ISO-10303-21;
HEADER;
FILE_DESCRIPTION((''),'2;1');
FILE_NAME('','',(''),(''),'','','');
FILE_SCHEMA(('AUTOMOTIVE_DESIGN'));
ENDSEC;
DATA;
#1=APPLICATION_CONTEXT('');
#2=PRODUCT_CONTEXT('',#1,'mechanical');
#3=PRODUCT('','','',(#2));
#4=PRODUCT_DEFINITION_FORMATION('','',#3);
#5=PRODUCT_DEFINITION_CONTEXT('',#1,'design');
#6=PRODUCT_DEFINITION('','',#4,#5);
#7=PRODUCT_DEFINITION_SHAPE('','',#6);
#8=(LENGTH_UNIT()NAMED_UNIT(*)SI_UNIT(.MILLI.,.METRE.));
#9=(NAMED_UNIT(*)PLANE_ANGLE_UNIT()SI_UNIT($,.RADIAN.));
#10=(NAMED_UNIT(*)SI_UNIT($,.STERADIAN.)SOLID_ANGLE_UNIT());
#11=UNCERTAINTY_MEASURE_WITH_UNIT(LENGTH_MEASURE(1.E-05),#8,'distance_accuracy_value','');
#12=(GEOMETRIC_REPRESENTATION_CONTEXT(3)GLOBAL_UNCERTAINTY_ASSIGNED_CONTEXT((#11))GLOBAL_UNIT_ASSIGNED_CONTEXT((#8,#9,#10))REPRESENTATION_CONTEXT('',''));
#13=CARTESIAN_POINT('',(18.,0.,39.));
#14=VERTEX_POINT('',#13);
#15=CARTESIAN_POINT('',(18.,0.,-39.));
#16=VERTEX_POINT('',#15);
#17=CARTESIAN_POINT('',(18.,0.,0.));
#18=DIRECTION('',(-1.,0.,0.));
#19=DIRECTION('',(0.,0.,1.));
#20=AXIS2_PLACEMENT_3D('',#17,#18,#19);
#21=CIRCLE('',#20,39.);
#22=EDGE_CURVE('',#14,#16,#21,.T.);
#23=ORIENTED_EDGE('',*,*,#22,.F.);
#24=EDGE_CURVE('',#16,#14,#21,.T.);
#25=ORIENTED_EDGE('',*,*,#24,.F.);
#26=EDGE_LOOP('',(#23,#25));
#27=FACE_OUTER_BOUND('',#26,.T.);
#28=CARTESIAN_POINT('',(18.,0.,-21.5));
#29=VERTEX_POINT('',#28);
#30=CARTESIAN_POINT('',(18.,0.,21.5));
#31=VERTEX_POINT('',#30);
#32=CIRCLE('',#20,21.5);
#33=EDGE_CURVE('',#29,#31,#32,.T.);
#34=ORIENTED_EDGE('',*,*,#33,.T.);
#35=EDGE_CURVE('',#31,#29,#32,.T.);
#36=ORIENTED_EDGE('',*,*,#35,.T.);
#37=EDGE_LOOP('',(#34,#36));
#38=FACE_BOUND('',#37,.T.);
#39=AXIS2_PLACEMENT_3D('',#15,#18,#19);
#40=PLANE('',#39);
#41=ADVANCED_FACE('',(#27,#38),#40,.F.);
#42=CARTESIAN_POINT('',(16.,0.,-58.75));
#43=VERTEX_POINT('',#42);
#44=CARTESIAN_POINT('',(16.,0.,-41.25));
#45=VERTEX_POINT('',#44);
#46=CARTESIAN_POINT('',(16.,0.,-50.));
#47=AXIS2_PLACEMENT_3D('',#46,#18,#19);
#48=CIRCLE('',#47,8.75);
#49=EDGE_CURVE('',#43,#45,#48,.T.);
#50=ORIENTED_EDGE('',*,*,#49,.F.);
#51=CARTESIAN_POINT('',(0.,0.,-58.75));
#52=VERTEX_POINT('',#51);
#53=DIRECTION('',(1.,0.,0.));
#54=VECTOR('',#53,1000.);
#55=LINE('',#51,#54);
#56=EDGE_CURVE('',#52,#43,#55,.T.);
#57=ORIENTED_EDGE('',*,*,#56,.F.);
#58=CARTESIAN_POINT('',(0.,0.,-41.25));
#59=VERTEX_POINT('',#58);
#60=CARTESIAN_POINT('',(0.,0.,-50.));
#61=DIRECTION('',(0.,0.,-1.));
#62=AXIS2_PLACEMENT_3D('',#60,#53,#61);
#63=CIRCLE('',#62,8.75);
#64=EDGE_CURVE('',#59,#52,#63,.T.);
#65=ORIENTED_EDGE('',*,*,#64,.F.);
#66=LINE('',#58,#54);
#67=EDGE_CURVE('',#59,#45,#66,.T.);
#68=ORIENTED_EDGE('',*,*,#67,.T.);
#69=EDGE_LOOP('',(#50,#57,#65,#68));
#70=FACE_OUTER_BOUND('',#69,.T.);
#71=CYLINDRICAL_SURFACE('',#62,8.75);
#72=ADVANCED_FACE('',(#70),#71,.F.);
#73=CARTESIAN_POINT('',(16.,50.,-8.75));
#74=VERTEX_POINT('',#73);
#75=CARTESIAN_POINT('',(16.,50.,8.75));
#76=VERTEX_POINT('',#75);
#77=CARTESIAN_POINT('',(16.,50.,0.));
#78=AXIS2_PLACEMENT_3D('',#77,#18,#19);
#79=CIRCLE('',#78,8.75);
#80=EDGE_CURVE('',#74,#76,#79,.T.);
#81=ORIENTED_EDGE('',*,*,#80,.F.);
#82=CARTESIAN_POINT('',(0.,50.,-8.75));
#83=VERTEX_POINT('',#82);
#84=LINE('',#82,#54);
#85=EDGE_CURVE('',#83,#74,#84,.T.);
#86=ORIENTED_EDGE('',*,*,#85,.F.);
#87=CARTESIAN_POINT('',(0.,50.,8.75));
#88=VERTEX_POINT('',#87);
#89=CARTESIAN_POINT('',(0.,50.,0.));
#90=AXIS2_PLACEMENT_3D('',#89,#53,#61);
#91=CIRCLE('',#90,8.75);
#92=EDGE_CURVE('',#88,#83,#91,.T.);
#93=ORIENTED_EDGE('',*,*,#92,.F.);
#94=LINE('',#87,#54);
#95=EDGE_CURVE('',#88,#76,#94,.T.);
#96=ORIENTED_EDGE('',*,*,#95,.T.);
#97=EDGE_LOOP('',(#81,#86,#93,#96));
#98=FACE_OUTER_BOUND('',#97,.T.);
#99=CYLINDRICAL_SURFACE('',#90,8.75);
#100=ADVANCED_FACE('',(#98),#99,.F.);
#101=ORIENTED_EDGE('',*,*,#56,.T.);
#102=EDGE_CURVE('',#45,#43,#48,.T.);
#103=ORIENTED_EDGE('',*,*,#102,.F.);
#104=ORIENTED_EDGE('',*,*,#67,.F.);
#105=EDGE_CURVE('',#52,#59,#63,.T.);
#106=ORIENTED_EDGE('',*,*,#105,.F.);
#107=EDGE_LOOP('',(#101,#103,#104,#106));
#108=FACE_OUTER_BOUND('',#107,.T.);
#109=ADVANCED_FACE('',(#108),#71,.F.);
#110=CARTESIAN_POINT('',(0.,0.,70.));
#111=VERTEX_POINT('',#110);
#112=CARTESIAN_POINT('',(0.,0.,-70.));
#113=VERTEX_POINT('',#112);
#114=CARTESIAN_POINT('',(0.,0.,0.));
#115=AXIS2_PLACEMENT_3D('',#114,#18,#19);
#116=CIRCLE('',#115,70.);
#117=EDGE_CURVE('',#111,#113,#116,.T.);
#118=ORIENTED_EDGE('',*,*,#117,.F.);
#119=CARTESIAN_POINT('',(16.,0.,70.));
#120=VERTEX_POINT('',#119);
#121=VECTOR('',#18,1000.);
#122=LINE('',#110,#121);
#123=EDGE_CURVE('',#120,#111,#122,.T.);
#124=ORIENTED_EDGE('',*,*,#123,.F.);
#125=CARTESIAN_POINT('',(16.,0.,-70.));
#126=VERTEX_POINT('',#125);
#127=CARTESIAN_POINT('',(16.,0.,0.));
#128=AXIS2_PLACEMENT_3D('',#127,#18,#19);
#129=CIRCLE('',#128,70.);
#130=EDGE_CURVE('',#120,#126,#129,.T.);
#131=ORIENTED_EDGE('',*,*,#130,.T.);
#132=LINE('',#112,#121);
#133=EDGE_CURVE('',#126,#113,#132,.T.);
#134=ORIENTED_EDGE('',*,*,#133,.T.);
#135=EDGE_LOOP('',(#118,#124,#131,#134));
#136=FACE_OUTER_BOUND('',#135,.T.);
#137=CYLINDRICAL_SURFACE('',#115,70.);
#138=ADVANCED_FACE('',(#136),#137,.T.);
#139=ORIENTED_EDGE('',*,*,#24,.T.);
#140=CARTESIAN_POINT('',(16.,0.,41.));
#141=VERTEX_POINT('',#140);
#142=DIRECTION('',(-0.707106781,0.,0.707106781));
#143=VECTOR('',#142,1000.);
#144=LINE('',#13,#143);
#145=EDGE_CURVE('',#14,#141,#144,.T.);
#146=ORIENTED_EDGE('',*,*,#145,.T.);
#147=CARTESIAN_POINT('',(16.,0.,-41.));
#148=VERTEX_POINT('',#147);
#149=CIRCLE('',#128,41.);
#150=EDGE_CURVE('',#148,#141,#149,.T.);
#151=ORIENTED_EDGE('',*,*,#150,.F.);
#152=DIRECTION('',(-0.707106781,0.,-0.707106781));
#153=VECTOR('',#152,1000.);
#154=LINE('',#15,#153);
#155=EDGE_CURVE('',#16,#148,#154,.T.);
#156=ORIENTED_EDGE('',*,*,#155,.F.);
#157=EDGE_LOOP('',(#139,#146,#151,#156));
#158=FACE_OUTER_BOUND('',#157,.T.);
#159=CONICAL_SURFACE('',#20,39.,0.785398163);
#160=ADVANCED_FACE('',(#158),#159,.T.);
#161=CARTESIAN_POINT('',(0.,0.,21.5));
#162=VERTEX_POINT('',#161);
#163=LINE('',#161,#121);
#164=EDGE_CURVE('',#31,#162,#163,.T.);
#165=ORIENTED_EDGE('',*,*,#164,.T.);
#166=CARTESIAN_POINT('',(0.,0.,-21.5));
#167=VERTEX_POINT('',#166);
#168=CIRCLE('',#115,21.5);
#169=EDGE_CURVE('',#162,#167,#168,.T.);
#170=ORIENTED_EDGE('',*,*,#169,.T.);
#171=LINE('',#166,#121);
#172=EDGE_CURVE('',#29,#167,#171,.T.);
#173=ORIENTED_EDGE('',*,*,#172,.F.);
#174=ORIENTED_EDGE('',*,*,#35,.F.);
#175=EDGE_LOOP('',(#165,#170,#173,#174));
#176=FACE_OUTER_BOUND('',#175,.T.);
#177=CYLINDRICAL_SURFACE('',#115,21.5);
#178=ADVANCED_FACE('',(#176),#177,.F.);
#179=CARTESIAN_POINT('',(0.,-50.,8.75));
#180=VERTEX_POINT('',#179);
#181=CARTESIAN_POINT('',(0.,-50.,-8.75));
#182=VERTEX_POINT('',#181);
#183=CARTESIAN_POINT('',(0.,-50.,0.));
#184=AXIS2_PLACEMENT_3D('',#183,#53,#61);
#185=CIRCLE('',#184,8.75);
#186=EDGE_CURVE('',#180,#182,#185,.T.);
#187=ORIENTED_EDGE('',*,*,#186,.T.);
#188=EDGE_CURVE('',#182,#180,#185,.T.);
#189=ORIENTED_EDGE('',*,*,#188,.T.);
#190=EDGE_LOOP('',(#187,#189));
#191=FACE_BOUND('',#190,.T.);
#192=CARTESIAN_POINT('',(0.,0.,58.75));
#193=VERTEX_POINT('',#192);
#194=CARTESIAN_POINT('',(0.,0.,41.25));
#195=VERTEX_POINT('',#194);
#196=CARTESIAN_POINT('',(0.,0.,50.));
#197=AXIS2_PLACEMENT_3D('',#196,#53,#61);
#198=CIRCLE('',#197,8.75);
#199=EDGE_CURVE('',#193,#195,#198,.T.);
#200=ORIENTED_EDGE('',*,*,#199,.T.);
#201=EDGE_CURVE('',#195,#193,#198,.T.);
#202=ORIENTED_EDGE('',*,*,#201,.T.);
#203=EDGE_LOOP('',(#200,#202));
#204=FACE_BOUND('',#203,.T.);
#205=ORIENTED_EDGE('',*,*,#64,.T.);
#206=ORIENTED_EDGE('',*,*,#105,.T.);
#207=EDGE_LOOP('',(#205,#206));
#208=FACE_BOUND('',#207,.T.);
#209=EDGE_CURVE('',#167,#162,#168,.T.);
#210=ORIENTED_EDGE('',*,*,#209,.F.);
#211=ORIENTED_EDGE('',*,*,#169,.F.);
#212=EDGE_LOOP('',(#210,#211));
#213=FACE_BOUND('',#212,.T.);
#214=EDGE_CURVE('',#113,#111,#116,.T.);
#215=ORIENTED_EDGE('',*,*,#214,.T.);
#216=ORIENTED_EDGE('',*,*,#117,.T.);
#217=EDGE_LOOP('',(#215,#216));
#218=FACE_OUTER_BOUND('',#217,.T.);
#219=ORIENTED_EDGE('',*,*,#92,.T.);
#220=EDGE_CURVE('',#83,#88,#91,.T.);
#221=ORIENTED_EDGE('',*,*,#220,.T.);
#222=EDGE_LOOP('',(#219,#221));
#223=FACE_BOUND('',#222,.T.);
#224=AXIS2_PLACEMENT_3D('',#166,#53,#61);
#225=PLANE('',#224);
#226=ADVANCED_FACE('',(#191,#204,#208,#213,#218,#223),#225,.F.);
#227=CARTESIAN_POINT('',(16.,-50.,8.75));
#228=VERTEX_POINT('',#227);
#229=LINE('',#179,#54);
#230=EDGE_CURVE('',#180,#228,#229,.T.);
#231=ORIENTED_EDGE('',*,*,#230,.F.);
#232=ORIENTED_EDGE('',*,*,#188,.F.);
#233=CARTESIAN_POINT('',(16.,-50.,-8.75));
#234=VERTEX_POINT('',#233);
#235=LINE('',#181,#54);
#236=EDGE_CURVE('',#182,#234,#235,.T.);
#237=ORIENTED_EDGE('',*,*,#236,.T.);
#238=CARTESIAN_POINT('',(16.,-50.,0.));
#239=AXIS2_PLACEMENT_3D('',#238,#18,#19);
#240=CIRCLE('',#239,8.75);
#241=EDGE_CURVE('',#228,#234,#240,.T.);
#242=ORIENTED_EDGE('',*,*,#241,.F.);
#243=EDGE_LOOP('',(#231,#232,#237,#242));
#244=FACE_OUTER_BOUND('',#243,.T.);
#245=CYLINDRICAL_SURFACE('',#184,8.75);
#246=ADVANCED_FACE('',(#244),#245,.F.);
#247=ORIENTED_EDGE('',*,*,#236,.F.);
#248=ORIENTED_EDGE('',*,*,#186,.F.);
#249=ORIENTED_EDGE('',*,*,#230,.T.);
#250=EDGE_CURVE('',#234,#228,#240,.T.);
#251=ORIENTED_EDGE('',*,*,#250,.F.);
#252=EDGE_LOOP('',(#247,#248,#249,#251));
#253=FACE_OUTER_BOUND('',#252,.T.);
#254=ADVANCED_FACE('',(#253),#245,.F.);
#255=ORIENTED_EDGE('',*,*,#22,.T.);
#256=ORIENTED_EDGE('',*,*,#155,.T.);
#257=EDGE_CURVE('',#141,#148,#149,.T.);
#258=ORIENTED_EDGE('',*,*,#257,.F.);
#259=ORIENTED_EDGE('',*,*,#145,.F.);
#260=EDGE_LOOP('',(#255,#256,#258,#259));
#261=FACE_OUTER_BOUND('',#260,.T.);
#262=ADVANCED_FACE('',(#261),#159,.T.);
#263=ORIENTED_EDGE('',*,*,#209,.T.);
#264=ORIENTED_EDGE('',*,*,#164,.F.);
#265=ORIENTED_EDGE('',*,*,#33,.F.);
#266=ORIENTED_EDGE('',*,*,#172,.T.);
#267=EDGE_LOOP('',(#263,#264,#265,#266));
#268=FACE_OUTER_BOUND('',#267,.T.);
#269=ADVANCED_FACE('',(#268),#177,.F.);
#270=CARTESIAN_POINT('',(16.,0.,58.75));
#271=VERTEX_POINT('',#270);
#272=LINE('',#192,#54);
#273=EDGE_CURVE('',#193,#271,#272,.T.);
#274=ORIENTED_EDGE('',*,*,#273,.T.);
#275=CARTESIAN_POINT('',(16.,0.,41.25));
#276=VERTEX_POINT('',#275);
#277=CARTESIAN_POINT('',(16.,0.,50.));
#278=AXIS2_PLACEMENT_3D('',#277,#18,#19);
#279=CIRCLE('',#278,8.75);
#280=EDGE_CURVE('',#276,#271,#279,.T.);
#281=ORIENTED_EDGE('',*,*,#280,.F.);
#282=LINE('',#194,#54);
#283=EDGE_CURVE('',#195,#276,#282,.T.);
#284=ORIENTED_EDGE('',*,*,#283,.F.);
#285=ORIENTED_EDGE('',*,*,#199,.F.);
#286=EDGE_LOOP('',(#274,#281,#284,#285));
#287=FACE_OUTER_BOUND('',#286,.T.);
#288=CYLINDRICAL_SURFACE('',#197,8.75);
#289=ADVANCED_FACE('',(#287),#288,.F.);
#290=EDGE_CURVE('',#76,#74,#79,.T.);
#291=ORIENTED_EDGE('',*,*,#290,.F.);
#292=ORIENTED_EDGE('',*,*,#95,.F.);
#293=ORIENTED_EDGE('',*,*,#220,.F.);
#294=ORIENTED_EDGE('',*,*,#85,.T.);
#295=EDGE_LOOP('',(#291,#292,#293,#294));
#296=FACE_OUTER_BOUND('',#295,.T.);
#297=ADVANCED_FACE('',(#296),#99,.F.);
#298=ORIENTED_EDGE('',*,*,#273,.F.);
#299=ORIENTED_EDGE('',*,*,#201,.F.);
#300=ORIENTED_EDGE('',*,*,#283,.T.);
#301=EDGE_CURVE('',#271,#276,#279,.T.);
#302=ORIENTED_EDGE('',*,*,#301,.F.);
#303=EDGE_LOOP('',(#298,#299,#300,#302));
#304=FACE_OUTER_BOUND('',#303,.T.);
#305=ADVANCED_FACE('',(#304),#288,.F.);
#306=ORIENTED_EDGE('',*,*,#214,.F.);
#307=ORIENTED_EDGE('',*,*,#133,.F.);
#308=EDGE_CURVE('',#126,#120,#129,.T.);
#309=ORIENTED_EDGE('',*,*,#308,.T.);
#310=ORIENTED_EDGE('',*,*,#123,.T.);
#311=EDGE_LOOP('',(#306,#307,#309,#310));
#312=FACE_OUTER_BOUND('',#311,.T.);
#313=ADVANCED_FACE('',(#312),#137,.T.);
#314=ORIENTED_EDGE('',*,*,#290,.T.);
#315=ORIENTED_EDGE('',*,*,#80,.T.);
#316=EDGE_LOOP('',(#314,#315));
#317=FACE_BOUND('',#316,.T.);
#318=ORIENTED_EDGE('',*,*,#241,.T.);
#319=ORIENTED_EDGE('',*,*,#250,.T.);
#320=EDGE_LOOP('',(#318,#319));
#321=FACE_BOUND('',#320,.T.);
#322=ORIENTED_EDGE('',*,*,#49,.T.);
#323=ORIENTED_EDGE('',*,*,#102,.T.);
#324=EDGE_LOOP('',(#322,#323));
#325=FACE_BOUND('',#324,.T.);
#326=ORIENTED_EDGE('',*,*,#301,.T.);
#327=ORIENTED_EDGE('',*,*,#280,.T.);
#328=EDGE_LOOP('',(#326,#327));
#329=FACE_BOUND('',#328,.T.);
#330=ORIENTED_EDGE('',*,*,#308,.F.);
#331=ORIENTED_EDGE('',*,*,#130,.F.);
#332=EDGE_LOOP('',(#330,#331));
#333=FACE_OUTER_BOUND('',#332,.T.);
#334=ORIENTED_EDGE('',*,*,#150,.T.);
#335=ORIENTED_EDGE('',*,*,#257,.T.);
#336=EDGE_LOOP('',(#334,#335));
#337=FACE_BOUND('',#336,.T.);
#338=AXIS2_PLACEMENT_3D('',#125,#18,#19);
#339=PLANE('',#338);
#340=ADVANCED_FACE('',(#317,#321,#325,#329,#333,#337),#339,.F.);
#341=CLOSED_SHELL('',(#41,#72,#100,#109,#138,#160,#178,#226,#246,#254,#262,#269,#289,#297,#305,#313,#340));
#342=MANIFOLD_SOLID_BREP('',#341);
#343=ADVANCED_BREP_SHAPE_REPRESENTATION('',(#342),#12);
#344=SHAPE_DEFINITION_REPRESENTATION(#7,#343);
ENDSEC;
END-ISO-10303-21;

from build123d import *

# Parameters (mm, degrees)
CUT_EXTRUDE_1_DEPTH      = 101.279609094
CUT_EXTRUDE_1_DEPTH_BACK = 101.279609094
SKETCH_2_R               = 8.75


with BuildPart() as part:
    # 草图1 → 旋转1 (revolve)
    with BuildSketch(Plane(origin=(0, 0, 0), x_dir=(1, 0, 0), z_dir=(0, 1, 0)), mode=Mode.PRIVATE) as revolve_1_sk:
        Polygon((0, 21.5), (0, 70), (16, 70), (16, 41), (18, 39), (18, 21.5), align=None)
    revolve(revolve_1_sk.sketch.rotate(Axis((0, 0, 0), (1, 0, 0)), 180), axis=Axis((0, 0, 0), (1, 0, 0)))

    # 草图2 → 切除-拉伸1 (cut, two sides: drawn at the far end of the back side and taken through both)
    with BuildSketch(Plane(origin=(16, 0, 0), x_dir=(0, 0, -1), z_dir=(1, 0, 0)).offset(-CUT_EXTRUDE_1_DEPTH_BACK)):
        with Locations((0, 50)):
            Circle(SKETCH_2_R)
        with Locations((50, 0)):
            Circle(SKETCH_2_R)
        with Locations((0, -50)):
            Circle(SKETCH_2_R)
        with Locations((-50, 0)):
            Circle(SKETCH_2_R)
    extrude(amount=CUT_EXTRUDE_1_DEPTH + CUT_EXTRUDE_1_DEPTH_BACK, mode=Mode.SUBTRACT)


solid = part.part
